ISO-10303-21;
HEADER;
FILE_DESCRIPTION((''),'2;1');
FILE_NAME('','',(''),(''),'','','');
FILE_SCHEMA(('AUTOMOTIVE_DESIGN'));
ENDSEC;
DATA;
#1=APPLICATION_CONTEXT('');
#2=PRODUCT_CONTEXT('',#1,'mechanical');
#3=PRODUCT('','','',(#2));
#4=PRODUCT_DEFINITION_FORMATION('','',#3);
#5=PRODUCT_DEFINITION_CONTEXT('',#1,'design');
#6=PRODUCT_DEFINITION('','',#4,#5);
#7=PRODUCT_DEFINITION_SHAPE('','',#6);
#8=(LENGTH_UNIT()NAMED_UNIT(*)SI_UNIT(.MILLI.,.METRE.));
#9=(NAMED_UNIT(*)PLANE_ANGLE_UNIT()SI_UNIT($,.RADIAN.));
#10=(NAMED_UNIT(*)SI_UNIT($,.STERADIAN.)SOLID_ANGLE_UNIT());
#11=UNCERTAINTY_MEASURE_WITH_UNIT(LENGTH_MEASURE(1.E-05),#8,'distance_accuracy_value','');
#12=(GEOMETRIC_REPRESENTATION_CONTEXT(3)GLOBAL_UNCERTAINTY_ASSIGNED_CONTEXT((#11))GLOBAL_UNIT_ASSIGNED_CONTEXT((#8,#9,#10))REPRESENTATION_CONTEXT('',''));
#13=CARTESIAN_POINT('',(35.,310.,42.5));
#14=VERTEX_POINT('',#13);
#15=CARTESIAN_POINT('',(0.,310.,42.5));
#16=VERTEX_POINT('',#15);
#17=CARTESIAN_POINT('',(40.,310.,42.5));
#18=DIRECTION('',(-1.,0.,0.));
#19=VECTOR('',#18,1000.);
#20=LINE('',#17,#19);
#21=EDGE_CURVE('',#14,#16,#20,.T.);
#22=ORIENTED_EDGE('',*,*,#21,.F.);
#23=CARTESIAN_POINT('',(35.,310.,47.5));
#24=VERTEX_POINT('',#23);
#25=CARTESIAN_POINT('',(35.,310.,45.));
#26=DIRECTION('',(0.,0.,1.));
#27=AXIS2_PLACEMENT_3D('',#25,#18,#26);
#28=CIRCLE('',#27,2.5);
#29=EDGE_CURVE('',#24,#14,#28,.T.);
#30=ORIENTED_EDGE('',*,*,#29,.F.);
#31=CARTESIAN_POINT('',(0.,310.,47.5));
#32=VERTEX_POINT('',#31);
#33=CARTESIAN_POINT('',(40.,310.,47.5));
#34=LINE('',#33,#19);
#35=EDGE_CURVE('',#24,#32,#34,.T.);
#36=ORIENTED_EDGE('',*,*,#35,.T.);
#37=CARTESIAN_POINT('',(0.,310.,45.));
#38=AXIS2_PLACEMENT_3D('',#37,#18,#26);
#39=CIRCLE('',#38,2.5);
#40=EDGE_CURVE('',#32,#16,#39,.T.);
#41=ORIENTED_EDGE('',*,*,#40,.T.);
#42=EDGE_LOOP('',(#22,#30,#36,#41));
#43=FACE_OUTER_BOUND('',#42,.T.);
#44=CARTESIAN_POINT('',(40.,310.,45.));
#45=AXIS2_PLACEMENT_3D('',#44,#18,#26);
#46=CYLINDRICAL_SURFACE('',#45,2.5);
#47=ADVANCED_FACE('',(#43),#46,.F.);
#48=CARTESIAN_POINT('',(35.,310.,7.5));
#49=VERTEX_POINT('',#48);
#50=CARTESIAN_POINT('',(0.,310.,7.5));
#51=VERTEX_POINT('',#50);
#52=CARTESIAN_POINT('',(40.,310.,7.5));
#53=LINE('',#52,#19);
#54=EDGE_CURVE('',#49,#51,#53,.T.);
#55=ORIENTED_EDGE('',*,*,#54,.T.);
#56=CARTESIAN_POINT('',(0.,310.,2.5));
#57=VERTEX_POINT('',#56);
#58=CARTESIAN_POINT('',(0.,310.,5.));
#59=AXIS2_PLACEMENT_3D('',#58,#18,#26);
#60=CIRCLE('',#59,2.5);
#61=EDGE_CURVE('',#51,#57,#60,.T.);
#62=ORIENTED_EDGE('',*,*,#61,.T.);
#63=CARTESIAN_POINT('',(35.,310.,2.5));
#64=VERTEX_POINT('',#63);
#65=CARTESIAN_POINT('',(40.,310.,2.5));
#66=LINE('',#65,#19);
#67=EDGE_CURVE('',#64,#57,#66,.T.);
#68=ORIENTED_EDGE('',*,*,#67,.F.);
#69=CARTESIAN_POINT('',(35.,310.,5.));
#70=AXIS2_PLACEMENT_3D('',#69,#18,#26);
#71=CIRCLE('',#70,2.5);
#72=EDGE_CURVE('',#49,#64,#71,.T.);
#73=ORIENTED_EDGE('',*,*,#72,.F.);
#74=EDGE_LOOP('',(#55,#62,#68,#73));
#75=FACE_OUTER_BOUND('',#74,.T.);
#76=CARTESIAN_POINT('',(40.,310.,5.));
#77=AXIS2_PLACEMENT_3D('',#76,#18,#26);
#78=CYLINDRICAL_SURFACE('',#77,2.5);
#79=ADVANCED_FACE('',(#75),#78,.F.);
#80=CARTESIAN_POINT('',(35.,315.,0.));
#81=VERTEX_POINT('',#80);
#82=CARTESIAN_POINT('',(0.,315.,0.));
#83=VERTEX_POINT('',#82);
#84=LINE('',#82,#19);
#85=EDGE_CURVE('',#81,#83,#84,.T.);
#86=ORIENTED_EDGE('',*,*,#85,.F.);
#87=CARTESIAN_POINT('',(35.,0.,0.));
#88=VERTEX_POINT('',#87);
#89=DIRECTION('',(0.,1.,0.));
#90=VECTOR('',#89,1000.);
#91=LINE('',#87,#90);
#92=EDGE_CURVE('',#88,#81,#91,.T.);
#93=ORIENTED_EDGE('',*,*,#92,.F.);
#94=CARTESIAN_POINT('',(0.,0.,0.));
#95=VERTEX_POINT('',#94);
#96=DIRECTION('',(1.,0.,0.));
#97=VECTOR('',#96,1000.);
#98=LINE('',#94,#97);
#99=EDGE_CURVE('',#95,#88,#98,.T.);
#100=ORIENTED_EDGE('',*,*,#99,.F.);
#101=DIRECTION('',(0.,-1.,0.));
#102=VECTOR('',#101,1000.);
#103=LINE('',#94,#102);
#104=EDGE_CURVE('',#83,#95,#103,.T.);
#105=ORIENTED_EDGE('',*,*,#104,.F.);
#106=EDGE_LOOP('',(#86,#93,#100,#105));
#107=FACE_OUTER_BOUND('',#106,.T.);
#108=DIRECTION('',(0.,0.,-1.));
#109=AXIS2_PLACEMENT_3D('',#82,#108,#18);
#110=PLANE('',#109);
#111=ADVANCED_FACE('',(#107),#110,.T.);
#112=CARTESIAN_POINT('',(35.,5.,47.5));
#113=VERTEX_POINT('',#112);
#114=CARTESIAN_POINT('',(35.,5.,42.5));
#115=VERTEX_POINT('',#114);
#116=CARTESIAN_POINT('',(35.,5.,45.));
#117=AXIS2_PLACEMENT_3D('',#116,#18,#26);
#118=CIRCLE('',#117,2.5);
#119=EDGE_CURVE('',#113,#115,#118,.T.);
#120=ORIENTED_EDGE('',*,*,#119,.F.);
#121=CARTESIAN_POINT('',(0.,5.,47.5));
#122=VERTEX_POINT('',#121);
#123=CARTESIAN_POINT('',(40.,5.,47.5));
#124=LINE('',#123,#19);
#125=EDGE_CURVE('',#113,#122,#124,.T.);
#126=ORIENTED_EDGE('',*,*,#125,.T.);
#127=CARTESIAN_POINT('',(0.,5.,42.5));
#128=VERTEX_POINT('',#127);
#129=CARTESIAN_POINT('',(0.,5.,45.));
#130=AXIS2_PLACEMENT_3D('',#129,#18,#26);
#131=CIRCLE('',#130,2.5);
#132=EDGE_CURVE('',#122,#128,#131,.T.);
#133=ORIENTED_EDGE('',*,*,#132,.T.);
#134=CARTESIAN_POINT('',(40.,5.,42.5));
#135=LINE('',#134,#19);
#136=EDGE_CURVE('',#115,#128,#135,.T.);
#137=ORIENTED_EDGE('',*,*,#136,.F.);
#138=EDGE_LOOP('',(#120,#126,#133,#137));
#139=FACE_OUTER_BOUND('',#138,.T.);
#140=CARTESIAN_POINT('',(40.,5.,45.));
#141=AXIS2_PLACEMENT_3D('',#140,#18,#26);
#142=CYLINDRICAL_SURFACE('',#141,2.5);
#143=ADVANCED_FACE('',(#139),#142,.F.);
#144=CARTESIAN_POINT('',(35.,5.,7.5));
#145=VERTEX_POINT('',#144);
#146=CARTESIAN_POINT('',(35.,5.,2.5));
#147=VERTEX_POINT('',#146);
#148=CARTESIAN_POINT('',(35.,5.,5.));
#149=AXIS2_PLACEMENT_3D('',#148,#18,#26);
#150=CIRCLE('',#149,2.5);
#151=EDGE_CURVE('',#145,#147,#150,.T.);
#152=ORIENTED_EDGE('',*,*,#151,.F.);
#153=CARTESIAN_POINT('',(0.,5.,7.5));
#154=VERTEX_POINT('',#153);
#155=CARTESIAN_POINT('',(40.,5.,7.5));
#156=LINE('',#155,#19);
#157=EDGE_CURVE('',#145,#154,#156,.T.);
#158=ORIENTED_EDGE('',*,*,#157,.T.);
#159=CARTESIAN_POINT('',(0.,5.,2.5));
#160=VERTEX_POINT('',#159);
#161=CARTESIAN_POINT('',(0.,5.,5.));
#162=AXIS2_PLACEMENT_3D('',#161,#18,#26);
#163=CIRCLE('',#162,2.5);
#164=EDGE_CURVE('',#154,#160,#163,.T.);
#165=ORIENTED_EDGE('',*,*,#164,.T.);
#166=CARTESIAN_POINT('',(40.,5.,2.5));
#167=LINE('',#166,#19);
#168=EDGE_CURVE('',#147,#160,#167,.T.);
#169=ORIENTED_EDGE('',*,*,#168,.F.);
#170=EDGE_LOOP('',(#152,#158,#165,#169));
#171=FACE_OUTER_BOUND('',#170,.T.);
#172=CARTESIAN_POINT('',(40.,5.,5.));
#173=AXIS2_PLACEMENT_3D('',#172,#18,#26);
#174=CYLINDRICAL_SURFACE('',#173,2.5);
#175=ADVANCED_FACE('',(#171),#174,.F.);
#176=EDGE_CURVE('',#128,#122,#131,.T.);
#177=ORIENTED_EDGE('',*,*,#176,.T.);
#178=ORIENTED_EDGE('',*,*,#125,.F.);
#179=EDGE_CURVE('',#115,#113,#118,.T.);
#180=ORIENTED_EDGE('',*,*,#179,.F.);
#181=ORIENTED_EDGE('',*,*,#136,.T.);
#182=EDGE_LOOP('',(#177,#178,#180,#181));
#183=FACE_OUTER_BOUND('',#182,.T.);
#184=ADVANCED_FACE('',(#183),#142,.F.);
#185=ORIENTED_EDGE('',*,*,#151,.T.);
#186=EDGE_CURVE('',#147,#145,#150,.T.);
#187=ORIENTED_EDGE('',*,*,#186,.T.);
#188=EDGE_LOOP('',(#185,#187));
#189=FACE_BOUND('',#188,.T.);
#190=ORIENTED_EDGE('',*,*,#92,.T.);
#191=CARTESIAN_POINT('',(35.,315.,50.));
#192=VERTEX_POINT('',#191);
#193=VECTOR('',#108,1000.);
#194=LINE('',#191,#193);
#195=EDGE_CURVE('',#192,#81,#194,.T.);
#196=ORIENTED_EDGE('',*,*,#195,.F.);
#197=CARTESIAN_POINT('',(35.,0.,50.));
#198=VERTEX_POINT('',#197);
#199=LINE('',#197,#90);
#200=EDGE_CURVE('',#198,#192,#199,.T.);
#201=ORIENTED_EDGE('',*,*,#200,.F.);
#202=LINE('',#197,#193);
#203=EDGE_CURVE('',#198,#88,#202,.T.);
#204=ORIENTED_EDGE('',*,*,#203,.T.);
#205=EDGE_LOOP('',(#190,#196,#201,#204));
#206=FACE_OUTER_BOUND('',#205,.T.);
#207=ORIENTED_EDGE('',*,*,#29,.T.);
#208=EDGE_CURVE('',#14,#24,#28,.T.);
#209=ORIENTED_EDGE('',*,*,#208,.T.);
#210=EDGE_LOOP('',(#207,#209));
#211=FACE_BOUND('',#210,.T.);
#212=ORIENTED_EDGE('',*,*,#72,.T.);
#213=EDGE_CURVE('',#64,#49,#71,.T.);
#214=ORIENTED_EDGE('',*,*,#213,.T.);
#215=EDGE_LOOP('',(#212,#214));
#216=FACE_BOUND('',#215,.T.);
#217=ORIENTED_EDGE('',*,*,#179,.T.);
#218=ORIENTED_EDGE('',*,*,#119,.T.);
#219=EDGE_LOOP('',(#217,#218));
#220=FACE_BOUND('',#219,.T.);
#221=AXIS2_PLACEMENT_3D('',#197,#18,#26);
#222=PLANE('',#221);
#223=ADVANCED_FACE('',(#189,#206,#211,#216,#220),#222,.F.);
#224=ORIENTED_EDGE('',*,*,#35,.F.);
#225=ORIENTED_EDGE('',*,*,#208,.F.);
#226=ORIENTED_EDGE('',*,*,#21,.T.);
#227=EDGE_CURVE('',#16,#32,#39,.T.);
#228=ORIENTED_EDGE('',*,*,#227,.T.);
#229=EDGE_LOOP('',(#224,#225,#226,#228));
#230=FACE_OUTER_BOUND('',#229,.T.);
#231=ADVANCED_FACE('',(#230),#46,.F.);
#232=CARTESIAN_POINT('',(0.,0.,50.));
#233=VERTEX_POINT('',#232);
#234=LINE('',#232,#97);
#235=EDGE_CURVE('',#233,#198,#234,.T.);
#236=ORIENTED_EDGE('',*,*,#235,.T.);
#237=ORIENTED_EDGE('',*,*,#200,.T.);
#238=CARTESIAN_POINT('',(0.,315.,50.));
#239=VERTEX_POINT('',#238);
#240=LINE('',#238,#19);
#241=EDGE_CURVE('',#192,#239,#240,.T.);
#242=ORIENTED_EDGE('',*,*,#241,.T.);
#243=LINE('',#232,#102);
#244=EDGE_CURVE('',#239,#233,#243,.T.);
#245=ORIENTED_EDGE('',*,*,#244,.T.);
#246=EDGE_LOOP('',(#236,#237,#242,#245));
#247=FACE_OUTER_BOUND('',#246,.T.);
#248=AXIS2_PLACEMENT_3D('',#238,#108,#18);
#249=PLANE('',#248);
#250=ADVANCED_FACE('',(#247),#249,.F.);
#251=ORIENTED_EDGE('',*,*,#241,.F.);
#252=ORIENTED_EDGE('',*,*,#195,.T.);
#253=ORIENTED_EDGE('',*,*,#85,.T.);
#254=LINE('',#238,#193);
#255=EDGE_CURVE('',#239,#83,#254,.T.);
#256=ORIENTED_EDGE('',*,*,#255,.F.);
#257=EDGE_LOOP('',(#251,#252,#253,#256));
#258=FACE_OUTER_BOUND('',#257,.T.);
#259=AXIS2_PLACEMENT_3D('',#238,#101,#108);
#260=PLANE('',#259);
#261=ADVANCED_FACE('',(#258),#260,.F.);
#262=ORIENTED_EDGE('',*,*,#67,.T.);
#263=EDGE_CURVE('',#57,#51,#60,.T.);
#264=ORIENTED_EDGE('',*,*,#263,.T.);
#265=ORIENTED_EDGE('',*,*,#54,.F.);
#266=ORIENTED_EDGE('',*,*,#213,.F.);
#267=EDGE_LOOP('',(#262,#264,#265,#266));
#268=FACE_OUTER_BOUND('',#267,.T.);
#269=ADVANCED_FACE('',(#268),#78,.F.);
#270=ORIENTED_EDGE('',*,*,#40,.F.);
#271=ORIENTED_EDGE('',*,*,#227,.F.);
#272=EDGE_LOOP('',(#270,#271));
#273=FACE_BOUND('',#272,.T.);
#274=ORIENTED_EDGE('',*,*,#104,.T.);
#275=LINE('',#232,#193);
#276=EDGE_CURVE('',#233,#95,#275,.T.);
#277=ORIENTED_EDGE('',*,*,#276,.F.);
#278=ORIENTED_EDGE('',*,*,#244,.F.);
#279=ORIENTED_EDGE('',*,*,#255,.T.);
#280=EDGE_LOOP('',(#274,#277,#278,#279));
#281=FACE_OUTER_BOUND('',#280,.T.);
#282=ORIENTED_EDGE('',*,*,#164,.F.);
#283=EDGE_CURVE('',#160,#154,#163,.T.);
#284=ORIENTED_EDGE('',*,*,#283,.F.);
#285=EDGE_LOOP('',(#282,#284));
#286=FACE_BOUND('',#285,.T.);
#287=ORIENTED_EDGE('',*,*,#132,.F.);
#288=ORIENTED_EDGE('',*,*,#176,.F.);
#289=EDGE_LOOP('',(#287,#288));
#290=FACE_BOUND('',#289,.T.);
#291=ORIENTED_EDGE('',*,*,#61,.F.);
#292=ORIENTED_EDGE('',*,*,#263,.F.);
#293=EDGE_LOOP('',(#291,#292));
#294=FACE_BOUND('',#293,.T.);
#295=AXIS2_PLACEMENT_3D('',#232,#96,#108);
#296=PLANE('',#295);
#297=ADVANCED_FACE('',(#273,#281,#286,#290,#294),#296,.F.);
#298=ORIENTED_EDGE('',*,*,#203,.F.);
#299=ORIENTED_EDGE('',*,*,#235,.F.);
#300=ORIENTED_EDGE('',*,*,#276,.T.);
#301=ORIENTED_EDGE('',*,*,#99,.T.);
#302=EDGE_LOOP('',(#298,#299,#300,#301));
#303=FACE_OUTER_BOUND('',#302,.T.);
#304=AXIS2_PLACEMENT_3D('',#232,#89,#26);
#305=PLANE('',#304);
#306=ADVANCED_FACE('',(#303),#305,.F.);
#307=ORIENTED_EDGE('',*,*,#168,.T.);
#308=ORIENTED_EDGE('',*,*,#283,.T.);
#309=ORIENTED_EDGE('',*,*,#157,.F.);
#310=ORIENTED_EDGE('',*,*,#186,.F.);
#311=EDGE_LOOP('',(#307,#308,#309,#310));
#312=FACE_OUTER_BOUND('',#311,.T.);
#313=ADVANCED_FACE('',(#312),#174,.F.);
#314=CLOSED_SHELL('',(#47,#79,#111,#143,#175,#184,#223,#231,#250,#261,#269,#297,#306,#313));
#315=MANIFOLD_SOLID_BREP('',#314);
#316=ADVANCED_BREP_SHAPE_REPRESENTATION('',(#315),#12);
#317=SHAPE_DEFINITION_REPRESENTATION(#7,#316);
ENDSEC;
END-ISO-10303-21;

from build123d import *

# Parameters (mm, degrees)
SKETCH_1_W          = 35
SKETCH_1_H          = 315
EXTRUDE_1_DEPTH     = 50
SKETCH_2_R          = 2.5
CUT_EXTRUDE_1_DEPTH = 40


with BuildPart() as part:
    # 草图1 → 凸台-拉伸1 (new body)
    with BuildSketch(Plane.XY):
        with Locations((17.5, 157.5)):
            Rectangle(SKETCH_1_W, SKETCH_1_H)
    extrude(amount=EXTRUDE_1_DEPTH)

    # 草图2 → 切除-拉伸1 (cut)
    with BuildSketch(Plane.ZY):
        with Locations((45, 310)):
            Circle(SKETCH_2_R)
        with Locations((5, 310)):
            Circle(SKETCH_2_R)
        with Locations((45, 5)):
            Circle(SKETCH_2_R)
        with Locations((5, 5)):
            Circle(SKETCH_2_R)
    extrude(amount=-CUT_EXTRUDE_1_DEPTH, mode=Mode.SUBTRACT)


solid = part.part
